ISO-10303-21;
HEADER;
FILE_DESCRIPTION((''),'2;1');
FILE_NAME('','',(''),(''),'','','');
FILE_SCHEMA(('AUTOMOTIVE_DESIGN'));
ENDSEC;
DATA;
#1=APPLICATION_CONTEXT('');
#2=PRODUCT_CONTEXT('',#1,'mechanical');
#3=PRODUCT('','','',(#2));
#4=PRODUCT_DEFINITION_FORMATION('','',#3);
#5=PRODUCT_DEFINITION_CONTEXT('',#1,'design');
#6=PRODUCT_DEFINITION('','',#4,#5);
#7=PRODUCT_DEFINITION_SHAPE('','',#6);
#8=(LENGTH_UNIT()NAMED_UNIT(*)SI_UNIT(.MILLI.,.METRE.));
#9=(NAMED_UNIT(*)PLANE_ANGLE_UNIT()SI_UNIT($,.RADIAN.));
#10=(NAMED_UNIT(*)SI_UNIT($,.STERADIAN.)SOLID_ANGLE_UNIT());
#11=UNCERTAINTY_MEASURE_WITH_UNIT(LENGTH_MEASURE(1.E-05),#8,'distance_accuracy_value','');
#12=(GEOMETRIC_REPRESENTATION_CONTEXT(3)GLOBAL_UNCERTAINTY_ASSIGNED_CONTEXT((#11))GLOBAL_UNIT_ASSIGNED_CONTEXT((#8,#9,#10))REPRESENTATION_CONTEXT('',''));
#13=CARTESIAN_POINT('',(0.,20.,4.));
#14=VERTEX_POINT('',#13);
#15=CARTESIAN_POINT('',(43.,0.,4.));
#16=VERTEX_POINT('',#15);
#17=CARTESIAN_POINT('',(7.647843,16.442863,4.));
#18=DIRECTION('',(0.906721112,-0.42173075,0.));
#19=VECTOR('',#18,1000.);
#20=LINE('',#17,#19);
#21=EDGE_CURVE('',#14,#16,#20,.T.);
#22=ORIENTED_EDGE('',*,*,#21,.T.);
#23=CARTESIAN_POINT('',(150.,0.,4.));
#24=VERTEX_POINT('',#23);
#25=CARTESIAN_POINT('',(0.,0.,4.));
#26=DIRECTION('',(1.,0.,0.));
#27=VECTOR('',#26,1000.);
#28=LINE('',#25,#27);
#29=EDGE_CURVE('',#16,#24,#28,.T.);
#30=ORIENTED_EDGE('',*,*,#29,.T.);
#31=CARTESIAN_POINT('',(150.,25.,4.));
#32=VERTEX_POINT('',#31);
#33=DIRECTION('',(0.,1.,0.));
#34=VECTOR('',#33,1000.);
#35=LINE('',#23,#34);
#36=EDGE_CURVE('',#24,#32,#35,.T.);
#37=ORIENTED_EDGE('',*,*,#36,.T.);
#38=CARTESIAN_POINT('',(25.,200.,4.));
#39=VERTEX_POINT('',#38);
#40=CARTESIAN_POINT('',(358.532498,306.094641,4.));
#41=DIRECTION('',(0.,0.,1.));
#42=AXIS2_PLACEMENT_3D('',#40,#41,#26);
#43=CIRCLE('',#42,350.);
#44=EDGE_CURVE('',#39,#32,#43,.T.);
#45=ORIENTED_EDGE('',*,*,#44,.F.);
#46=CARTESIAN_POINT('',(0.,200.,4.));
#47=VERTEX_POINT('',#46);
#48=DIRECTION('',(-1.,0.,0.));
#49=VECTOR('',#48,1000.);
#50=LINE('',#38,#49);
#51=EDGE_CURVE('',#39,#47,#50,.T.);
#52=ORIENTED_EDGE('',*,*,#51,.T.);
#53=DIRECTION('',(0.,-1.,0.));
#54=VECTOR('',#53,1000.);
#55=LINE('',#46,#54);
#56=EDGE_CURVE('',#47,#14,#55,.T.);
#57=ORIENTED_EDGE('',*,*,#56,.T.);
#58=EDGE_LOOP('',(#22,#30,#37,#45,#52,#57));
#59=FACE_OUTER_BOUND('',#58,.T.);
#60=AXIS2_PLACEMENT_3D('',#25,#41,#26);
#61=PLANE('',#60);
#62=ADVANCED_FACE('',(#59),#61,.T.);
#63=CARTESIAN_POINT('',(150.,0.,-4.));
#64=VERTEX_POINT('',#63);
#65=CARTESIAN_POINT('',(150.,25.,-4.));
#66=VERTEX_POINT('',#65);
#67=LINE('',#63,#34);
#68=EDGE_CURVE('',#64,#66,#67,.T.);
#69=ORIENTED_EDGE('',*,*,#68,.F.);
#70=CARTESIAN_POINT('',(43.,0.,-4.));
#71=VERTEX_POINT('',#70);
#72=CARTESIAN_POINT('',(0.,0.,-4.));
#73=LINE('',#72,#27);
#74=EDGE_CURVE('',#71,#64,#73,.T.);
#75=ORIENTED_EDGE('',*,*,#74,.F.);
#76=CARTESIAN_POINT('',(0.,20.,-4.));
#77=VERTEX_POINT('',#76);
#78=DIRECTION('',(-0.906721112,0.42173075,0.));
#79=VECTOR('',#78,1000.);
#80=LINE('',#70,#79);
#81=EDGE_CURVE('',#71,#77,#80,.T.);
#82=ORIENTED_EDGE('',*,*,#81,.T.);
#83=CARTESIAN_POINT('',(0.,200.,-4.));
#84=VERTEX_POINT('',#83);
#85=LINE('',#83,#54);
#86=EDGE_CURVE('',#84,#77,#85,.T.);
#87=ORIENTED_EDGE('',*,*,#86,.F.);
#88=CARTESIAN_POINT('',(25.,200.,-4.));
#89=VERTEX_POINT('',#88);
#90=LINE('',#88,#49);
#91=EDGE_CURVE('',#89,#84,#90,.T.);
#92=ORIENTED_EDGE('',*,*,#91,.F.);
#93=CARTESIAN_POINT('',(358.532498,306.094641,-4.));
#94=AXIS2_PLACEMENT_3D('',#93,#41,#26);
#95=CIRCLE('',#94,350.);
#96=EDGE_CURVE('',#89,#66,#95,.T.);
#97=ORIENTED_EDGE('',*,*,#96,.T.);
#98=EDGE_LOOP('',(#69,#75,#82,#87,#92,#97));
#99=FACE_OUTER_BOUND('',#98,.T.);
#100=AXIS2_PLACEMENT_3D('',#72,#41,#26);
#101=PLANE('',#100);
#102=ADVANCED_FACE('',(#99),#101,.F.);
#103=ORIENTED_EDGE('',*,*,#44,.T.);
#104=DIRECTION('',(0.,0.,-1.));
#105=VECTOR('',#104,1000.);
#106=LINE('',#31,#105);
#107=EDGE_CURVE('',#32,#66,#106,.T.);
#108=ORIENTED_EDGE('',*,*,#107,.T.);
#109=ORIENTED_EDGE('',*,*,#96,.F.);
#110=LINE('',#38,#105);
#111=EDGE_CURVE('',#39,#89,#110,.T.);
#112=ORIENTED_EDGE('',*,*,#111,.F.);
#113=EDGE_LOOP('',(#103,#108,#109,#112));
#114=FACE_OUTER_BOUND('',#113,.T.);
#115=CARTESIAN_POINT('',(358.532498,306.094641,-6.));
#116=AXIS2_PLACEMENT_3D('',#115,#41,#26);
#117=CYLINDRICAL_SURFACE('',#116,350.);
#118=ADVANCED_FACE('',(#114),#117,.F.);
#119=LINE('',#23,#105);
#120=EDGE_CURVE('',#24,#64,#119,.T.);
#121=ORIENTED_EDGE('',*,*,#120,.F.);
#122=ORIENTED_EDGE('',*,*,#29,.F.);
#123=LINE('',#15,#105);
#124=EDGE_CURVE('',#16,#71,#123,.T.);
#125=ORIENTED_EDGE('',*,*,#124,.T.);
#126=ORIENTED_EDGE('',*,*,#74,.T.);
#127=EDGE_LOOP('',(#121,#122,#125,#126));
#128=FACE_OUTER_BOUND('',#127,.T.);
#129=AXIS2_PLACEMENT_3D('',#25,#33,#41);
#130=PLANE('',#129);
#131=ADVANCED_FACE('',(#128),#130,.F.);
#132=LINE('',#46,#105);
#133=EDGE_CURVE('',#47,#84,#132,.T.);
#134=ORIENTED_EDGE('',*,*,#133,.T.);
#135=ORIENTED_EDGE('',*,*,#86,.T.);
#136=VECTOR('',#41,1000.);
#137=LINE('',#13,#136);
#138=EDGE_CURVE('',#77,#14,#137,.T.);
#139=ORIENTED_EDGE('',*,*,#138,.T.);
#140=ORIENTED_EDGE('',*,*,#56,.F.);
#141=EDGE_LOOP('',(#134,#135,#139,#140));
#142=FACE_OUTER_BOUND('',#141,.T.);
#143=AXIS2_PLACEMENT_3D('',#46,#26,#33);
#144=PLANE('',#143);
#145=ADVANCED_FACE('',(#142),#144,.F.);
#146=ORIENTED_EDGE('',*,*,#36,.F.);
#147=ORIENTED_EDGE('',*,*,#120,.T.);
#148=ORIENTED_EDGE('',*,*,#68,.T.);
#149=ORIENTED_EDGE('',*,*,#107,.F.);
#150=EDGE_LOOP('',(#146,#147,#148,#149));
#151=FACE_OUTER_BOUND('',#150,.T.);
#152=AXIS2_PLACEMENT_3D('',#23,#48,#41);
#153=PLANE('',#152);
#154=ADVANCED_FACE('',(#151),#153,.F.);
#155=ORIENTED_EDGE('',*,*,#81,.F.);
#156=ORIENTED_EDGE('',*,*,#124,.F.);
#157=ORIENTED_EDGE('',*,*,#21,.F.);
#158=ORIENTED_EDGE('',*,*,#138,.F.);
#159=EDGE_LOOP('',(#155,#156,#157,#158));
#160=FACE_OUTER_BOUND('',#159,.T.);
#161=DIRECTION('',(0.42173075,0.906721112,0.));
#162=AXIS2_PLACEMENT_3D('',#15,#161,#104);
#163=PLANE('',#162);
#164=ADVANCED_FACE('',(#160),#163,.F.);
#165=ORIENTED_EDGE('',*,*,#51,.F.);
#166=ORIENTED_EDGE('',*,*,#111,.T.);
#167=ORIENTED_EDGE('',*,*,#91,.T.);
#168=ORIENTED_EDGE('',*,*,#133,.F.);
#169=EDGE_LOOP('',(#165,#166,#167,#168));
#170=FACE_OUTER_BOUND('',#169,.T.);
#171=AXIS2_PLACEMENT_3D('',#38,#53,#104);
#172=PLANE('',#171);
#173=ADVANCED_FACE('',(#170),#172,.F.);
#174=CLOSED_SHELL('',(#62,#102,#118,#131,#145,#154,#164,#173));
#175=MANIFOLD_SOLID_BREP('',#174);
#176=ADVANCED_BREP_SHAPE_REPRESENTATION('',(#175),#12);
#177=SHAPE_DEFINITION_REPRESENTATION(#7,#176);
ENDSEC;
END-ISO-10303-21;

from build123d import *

# Parameters (mm, degrees)
BOSS_EXTRUDE1_DEPTH = 4
CHAMFER1_SIZE       = 20
CHAMFER1_SIZE2      = 43
CUT_EXTRUDE1_DEPTH  = 10


with BuildPart() as part:
    # Sketch1 → Boss-Extrude1 (new, symmetric)
    with BuildSketch(Plane.XY):
        Polygon((0, 0), (150, 0), (150, 25), (25, 200), (0, 200), align=None)
    extrude(amount=BOSS_EXTRUDE1_DEPTH, both=True)

    # Chamfer1
    chamfer1_edges = [part.edges().sort_by_distance(p)[0] for p in [
        (0, 0, 0),
    ]]
    chamfer1_side = [part.faces().sort_by_distance(p)[0] for p in [
        (0, 100, 0),
    ]]
    chamfer(chamfer1_edges, length=CHAMFER1_SIZE, length2=CHAMFER1_SIZE2, reference=chamfer1_side[0])

    # Sketch2 → Cut-Extrude1 (cut)
    with BuildSketch(Plane.XY.offset(4)):
        with BuildLine():
            ThreePointArc((25, 200), (73.72578288, 102.661273486), (150, 25))
            Line((150, 25), (25, 200))
        make_face()
    extrude(amount=-CUT_EXTRUDE1_DEPTH, mode=Mode.SUBTRACT)


solid = part.part
